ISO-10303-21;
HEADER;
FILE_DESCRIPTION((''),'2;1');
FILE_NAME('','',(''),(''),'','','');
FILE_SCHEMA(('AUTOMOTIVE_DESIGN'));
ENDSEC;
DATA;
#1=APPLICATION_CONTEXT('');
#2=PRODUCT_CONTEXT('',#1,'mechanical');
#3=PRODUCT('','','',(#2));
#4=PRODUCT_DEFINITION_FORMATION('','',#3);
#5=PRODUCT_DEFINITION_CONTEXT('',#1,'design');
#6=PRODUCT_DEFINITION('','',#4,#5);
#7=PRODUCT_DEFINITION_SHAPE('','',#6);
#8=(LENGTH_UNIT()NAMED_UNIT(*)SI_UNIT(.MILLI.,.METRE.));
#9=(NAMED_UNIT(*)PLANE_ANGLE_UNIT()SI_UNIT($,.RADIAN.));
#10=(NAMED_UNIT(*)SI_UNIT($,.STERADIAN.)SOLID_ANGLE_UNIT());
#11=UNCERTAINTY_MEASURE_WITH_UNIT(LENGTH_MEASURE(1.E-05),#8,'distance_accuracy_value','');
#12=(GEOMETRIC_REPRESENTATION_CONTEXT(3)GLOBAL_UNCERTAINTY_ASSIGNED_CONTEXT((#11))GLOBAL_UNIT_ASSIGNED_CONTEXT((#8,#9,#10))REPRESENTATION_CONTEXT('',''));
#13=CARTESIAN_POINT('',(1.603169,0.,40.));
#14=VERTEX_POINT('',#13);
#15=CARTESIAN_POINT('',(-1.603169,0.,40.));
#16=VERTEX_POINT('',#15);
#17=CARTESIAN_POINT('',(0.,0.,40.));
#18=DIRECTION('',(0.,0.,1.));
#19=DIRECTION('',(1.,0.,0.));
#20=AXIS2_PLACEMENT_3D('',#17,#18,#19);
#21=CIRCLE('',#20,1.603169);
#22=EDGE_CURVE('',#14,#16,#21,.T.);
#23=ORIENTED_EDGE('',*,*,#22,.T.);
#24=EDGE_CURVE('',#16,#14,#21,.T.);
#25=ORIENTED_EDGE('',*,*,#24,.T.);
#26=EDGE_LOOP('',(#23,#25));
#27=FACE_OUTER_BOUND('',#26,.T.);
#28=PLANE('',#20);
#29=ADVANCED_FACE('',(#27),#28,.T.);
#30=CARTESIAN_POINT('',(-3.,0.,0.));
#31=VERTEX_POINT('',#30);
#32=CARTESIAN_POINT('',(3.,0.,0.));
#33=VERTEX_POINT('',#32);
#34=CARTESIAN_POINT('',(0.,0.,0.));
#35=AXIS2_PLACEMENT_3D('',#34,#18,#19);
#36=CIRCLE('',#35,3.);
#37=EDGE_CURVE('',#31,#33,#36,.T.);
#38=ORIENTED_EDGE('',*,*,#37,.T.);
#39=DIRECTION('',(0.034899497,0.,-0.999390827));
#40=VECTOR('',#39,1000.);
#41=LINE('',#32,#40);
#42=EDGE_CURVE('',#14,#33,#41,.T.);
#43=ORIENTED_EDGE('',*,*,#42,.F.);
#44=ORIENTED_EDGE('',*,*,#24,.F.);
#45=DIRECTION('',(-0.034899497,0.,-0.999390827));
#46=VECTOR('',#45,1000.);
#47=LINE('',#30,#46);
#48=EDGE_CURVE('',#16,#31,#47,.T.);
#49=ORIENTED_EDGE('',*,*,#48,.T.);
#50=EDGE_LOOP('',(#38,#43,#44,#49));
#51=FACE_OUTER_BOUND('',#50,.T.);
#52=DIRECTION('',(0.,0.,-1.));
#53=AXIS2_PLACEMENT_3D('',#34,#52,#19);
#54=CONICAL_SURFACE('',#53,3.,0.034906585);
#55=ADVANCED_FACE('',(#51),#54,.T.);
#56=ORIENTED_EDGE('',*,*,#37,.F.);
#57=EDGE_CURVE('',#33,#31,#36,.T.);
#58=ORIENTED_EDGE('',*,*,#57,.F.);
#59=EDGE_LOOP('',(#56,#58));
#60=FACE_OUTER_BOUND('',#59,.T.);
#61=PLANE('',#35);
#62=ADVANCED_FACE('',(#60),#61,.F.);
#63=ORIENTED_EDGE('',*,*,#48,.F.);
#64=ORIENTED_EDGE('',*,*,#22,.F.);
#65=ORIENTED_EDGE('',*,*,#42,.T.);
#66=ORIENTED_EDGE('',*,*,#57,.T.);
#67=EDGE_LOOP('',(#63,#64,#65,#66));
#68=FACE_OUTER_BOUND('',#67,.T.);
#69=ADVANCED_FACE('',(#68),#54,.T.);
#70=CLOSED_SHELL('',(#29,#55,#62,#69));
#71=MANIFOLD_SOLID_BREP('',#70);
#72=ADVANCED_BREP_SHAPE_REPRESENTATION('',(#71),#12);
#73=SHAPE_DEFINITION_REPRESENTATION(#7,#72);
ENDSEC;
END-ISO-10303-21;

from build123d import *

# Parameters (mm, degrees)
PIN_PROFILE_6_R                   = 3
TAPER_PIN_BODY_40MM_2_DRAFT_DEPTH = 40
TAPER_PIN_BODY_40MM_2_DRAFT_TAPER = 2


with BuildPart() as part:
    # Pin Profile Ø6 → Taper Pin Body 40mm 2° Draft (new body)
    with BuildSketch(Plane.XY):
        Circle(PIN_PROFILE_6_R)
    extrude(amount=TAPER_PIN_BODY_40MM_2_DRAFT_DEPTH, taper=TAPER_PIN_BODY_40MM_2_DRAFT_TAPER)


solid = part.part
